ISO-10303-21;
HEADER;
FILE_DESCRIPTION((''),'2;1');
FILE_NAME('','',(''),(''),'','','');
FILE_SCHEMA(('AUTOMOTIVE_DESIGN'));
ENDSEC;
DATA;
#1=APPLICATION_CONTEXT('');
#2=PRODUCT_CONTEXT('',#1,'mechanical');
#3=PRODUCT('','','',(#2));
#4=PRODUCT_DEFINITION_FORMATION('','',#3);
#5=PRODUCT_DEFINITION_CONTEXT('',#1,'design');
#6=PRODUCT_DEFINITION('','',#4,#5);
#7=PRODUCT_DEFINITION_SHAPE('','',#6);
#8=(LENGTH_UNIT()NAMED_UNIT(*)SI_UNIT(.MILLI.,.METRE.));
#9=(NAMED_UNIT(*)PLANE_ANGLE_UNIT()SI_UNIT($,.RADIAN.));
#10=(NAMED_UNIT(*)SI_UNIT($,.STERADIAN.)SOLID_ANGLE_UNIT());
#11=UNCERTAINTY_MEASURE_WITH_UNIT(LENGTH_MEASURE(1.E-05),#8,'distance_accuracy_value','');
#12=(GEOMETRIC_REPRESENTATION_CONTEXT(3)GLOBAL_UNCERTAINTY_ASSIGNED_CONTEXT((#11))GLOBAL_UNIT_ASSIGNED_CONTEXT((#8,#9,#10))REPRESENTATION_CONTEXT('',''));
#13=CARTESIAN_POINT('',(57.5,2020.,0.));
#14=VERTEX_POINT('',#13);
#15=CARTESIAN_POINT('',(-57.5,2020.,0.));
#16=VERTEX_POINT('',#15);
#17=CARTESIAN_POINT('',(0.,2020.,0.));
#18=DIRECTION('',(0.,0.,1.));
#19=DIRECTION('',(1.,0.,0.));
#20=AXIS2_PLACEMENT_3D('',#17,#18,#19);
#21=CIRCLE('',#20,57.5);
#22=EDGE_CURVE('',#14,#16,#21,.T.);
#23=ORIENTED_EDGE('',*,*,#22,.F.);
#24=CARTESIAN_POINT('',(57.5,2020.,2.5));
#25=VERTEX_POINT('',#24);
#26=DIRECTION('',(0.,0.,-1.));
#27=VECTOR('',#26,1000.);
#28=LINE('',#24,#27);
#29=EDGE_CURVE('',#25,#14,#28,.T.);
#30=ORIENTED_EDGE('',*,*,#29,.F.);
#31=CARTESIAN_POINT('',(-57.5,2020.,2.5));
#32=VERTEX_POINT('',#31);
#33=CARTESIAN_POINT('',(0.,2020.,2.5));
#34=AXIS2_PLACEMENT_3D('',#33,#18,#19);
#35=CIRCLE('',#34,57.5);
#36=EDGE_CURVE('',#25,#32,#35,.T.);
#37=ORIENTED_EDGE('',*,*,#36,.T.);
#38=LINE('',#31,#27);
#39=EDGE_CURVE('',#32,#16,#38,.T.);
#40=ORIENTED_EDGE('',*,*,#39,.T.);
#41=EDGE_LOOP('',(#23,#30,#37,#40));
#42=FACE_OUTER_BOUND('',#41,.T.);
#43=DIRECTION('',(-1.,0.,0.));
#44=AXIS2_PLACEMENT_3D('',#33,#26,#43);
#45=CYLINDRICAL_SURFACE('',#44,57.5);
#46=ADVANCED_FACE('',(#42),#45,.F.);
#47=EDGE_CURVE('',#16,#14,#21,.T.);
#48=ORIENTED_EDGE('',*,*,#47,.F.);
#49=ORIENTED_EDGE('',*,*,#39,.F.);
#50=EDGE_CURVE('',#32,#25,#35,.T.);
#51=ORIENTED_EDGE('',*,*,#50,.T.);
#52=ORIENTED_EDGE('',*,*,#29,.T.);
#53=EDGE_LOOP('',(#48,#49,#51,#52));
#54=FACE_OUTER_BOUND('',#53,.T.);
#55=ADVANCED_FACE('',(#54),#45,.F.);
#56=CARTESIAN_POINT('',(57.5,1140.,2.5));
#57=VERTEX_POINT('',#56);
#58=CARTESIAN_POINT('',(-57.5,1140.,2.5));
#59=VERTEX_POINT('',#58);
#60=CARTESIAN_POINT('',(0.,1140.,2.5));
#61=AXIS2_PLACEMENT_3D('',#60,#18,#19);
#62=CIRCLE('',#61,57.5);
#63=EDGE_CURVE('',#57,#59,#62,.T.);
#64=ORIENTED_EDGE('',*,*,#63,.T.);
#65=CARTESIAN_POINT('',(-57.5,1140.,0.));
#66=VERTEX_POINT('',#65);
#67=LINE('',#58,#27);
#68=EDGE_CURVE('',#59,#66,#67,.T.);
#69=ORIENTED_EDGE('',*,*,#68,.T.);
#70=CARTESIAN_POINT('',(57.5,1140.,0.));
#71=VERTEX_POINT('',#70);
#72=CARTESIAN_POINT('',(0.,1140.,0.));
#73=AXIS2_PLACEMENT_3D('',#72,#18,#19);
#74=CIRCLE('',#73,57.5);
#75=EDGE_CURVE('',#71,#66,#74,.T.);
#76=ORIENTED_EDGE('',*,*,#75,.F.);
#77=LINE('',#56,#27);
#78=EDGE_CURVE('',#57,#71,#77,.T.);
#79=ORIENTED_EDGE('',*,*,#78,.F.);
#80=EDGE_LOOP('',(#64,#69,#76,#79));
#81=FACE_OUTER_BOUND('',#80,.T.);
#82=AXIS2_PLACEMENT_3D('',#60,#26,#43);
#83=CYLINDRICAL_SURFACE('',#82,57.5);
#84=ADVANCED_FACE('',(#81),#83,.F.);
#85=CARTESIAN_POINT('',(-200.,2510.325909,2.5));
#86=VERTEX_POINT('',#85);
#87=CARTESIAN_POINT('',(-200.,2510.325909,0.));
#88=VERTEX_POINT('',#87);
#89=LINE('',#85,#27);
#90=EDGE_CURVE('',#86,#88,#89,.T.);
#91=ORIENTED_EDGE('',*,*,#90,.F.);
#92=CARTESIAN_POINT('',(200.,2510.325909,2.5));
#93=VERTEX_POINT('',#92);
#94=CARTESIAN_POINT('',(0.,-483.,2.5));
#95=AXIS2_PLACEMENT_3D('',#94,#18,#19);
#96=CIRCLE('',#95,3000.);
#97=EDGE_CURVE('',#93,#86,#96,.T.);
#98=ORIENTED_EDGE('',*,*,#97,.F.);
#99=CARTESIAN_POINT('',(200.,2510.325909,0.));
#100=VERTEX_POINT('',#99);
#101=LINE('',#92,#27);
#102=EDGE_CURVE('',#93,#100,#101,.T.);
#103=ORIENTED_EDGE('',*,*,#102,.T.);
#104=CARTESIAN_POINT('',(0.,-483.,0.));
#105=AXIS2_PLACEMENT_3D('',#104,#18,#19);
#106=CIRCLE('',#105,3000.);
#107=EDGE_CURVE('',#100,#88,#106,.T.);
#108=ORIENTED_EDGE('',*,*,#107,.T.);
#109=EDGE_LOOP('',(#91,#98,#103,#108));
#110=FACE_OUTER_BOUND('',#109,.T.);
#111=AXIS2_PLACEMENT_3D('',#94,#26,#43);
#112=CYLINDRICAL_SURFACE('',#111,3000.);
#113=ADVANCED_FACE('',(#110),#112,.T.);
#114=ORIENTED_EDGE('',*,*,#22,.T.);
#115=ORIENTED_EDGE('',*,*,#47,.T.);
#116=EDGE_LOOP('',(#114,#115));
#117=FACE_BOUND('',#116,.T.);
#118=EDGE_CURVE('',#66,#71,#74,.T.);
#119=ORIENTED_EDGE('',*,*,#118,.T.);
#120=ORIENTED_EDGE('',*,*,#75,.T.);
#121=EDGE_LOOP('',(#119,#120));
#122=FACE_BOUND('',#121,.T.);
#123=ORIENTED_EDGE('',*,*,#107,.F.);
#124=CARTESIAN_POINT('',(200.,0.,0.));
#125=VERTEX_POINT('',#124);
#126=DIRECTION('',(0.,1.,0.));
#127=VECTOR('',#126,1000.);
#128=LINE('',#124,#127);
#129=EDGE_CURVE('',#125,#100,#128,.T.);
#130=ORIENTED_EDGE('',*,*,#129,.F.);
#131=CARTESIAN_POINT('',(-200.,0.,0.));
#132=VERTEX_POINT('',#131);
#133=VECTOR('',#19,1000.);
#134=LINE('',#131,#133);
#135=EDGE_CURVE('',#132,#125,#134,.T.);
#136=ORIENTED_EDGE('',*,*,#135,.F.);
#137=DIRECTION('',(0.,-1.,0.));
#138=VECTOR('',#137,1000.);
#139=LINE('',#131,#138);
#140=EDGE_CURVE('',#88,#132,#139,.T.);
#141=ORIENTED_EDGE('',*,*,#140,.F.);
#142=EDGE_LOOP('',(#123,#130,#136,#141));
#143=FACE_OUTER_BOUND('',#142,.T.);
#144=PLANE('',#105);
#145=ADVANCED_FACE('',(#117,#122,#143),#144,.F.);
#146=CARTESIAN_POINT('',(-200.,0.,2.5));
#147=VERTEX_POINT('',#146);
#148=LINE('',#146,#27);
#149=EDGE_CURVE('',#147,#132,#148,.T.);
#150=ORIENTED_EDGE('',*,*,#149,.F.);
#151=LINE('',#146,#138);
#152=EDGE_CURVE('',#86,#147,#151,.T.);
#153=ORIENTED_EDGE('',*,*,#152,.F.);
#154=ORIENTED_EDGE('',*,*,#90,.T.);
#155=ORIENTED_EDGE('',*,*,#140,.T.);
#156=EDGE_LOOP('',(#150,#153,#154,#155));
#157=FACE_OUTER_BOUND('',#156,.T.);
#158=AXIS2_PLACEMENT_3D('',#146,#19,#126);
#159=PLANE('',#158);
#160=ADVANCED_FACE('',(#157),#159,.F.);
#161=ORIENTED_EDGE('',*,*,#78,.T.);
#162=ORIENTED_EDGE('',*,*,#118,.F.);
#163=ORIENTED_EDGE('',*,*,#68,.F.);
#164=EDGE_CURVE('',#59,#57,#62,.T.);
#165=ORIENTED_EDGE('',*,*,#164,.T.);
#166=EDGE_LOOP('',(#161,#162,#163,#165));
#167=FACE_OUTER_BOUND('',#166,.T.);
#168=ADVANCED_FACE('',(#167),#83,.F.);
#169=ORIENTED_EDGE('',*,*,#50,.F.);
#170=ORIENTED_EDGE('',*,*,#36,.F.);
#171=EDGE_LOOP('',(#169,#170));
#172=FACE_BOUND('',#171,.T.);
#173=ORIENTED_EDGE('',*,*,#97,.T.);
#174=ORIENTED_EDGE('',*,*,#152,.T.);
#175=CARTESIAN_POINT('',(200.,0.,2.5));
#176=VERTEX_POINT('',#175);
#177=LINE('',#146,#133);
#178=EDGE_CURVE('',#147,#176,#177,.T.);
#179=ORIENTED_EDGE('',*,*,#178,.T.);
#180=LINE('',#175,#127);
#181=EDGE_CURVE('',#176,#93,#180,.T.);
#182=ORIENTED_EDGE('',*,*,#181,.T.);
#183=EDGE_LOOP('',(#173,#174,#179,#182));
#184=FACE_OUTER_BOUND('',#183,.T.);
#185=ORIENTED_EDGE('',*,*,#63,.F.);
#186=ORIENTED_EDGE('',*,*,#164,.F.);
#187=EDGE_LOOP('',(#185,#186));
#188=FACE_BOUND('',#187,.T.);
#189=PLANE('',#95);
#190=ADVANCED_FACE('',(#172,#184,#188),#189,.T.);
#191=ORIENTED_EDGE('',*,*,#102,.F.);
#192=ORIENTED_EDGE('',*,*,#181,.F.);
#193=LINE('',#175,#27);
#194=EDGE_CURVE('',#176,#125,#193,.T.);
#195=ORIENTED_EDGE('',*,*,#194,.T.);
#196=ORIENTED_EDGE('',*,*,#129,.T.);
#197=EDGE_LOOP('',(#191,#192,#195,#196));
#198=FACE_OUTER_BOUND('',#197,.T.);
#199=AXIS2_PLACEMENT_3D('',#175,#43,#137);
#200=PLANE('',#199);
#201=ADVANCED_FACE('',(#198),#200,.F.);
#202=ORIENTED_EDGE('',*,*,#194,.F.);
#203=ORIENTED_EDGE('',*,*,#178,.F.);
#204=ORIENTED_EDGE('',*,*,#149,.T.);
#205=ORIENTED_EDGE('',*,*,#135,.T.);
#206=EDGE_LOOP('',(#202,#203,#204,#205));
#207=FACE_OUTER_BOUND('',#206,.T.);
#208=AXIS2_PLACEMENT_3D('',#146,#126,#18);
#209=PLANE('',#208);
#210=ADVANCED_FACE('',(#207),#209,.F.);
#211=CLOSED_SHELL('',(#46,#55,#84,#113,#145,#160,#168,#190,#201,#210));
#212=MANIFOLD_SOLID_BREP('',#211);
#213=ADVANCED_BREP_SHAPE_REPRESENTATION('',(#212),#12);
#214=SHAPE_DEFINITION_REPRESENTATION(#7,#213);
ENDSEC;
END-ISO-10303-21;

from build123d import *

# Parameters (mm, degrees)
SKETCH1_R           = 57.5
BOSS_EXTRUDE1_DEPTH = 2.5


with BuildPart() as part:
    # Sketch1 → Boss-Extrude1 (new body)
    with BuildSketch(Plane.XY):
        with BuildLine():
            Line((-200, 0), (200, 0))
            Line((200, 0), (200, 2510.325909419))
            ThreePointArc((200, 2510.325909419), (0, 2517), (-200, 2510.325909419))
            Line((-200, 2510.325909419), (-200, 0))
        make_face()
        with Locations((0, 2020)):
            Circle(SKETCH1_R, mode=Mode.SUBTRACT)
        with Locations((0, 1140)):
            Circle(SKETCH1_R, mode=Mode.SUBTRACT)
    extrude(amount=BOSS_EXTRUDE1_DEPTH)


solid = part.part
